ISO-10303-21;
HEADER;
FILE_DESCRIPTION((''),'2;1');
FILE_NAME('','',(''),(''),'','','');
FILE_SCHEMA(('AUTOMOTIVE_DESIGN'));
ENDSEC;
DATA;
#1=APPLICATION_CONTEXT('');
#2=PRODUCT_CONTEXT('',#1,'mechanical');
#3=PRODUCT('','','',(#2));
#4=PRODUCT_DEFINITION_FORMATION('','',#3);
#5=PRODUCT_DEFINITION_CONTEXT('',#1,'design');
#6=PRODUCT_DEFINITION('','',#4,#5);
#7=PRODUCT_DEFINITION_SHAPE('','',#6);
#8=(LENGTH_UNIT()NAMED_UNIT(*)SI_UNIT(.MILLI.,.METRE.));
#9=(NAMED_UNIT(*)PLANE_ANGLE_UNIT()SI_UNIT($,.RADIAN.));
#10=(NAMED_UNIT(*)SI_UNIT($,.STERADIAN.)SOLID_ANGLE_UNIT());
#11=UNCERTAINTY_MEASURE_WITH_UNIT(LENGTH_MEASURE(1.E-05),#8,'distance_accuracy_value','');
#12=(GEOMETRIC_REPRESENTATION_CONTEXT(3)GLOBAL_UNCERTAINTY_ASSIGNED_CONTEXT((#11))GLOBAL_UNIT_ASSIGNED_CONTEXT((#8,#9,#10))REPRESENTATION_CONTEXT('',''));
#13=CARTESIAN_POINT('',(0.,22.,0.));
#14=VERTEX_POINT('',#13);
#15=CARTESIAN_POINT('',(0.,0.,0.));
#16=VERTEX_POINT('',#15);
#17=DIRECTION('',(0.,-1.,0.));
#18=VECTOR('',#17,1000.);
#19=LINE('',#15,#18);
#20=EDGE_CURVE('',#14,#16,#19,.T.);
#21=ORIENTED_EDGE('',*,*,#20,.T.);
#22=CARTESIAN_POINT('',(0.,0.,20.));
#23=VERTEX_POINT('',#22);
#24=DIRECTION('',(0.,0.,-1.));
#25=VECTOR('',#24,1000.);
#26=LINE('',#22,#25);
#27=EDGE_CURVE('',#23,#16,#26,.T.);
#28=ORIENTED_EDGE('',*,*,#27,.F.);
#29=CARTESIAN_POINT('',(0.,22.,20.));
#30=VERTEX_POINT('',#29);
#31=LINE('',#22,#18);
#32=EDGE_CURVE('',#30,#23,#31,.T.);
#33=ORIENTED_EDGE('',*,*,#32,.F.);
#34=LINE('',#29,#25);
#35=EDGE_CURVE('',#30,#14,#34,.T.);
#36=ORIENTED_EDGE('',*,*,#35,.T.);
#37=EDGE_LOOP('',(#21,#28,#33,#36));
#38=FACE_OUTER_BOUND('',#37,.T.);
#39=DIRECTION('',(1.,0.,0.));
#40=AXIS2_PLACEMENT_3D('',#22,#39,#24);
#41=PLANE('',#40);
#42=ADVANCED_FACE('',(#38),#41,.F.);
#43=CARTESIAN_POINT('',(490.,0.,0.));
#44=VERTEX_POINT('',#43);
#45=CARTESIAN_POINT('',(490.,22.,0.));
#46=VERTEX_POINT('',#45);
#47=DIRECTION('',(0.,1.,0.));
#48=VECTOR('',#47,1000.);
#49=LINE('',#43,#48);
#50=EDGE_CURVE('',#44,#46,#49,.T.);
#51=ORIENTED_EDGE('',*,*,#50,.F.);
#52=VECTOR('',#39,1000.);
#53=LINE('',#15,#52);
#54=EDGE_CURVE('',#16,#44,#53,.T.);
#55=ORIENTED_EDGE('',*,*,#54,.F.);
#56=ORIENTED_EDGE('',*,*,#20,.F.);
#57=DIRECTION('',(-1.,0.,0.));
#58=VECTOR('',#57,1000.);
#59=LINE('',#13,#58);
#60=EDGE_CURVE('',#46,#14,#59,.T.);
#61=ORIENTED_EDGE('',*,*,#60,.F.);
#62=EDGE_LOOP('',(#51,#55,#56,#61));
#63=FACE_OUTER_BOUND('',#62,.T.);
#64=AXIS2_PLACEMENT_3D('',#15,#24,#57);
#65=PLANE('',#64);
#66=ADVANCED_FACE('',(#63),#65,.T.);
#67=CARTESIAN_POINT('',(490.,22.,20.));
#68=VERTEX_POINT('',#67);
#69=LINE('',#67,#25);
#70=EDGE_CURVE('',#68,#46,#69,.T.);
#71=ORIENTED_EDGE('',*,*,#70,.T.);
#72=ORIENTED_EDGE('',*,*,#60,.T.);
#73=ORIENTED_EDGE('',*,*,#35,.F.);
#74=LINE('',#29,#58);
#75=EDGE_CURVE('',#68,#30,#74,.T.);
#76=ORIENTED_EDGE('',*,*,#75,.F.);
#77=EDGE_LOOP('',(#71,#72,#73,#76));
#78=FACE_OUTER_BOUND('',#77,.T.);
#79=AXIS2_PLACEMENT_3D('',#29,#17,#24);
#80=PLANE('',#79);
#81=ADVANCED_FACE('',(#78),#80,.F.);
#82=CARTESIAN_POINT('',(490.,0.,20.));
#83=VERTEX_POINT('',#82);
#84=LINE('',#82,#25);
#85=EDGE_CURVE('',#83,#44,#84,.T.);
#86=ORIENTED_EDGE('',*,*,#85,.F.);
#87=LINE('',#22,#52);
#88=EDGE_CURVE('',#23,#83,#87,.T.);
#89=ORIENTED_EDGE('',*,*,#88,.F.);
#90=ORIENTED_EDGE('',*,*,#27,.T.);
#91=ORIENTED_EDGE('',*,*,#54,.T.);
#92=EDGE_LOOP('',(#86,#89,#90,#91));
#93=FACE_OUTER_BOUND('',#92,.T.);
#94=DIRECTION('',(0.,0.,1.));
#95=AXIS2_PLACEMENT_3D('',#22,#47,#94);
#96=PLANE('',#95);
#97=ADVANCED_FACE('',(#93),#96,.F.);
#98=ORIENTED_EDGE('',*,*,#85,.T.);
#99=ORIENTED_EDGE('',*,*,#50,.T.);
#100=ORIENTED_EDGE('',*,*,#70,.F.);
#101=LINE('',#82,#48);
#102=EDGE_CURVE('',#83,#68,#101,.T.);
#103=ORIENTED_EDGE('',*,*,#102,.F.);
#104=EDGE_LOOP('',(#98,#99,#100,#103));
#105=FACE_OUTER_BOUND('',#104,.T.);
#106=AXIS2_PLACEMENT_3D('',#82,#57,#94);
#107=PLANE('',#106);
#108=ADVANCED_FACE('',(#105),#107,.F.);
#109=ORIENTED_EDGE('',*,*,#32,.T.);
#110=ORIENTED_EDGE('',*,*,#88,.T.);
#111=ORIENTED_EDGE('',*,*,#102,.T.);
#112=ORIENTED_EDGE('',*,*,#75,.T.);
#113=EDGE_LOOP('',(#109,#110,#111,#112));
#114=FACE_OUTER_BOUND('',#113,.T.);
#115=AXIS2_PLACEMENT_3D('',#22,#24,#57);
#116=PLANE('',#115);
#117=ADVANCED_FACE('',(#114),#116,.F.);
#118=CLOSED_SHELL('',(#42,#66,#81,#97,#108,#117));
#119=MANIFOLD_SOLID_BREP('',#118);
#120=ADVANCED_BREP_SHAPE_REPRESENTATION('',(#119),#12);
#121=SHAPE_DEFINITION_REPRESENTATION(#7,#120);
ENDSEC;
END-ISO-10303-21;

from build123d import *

# Parameters (mm, degrees)
SKETCH1_W           = 490
SKETCH1_H           = 22
BOSS_EXTRUDE1_DEPTH = 20


with BuildPart() as part:
    # Sketch1 → Boss-Extrude1 (new body)
    with BuildSketch(Plane.XY):
        with Locations((245, 11)):
            Rectangle(SKETCH1_W, SKETCH1_H)
    extrude(amount=BOSS_EXTRUDE1_DEPTH)


solid = part.part
